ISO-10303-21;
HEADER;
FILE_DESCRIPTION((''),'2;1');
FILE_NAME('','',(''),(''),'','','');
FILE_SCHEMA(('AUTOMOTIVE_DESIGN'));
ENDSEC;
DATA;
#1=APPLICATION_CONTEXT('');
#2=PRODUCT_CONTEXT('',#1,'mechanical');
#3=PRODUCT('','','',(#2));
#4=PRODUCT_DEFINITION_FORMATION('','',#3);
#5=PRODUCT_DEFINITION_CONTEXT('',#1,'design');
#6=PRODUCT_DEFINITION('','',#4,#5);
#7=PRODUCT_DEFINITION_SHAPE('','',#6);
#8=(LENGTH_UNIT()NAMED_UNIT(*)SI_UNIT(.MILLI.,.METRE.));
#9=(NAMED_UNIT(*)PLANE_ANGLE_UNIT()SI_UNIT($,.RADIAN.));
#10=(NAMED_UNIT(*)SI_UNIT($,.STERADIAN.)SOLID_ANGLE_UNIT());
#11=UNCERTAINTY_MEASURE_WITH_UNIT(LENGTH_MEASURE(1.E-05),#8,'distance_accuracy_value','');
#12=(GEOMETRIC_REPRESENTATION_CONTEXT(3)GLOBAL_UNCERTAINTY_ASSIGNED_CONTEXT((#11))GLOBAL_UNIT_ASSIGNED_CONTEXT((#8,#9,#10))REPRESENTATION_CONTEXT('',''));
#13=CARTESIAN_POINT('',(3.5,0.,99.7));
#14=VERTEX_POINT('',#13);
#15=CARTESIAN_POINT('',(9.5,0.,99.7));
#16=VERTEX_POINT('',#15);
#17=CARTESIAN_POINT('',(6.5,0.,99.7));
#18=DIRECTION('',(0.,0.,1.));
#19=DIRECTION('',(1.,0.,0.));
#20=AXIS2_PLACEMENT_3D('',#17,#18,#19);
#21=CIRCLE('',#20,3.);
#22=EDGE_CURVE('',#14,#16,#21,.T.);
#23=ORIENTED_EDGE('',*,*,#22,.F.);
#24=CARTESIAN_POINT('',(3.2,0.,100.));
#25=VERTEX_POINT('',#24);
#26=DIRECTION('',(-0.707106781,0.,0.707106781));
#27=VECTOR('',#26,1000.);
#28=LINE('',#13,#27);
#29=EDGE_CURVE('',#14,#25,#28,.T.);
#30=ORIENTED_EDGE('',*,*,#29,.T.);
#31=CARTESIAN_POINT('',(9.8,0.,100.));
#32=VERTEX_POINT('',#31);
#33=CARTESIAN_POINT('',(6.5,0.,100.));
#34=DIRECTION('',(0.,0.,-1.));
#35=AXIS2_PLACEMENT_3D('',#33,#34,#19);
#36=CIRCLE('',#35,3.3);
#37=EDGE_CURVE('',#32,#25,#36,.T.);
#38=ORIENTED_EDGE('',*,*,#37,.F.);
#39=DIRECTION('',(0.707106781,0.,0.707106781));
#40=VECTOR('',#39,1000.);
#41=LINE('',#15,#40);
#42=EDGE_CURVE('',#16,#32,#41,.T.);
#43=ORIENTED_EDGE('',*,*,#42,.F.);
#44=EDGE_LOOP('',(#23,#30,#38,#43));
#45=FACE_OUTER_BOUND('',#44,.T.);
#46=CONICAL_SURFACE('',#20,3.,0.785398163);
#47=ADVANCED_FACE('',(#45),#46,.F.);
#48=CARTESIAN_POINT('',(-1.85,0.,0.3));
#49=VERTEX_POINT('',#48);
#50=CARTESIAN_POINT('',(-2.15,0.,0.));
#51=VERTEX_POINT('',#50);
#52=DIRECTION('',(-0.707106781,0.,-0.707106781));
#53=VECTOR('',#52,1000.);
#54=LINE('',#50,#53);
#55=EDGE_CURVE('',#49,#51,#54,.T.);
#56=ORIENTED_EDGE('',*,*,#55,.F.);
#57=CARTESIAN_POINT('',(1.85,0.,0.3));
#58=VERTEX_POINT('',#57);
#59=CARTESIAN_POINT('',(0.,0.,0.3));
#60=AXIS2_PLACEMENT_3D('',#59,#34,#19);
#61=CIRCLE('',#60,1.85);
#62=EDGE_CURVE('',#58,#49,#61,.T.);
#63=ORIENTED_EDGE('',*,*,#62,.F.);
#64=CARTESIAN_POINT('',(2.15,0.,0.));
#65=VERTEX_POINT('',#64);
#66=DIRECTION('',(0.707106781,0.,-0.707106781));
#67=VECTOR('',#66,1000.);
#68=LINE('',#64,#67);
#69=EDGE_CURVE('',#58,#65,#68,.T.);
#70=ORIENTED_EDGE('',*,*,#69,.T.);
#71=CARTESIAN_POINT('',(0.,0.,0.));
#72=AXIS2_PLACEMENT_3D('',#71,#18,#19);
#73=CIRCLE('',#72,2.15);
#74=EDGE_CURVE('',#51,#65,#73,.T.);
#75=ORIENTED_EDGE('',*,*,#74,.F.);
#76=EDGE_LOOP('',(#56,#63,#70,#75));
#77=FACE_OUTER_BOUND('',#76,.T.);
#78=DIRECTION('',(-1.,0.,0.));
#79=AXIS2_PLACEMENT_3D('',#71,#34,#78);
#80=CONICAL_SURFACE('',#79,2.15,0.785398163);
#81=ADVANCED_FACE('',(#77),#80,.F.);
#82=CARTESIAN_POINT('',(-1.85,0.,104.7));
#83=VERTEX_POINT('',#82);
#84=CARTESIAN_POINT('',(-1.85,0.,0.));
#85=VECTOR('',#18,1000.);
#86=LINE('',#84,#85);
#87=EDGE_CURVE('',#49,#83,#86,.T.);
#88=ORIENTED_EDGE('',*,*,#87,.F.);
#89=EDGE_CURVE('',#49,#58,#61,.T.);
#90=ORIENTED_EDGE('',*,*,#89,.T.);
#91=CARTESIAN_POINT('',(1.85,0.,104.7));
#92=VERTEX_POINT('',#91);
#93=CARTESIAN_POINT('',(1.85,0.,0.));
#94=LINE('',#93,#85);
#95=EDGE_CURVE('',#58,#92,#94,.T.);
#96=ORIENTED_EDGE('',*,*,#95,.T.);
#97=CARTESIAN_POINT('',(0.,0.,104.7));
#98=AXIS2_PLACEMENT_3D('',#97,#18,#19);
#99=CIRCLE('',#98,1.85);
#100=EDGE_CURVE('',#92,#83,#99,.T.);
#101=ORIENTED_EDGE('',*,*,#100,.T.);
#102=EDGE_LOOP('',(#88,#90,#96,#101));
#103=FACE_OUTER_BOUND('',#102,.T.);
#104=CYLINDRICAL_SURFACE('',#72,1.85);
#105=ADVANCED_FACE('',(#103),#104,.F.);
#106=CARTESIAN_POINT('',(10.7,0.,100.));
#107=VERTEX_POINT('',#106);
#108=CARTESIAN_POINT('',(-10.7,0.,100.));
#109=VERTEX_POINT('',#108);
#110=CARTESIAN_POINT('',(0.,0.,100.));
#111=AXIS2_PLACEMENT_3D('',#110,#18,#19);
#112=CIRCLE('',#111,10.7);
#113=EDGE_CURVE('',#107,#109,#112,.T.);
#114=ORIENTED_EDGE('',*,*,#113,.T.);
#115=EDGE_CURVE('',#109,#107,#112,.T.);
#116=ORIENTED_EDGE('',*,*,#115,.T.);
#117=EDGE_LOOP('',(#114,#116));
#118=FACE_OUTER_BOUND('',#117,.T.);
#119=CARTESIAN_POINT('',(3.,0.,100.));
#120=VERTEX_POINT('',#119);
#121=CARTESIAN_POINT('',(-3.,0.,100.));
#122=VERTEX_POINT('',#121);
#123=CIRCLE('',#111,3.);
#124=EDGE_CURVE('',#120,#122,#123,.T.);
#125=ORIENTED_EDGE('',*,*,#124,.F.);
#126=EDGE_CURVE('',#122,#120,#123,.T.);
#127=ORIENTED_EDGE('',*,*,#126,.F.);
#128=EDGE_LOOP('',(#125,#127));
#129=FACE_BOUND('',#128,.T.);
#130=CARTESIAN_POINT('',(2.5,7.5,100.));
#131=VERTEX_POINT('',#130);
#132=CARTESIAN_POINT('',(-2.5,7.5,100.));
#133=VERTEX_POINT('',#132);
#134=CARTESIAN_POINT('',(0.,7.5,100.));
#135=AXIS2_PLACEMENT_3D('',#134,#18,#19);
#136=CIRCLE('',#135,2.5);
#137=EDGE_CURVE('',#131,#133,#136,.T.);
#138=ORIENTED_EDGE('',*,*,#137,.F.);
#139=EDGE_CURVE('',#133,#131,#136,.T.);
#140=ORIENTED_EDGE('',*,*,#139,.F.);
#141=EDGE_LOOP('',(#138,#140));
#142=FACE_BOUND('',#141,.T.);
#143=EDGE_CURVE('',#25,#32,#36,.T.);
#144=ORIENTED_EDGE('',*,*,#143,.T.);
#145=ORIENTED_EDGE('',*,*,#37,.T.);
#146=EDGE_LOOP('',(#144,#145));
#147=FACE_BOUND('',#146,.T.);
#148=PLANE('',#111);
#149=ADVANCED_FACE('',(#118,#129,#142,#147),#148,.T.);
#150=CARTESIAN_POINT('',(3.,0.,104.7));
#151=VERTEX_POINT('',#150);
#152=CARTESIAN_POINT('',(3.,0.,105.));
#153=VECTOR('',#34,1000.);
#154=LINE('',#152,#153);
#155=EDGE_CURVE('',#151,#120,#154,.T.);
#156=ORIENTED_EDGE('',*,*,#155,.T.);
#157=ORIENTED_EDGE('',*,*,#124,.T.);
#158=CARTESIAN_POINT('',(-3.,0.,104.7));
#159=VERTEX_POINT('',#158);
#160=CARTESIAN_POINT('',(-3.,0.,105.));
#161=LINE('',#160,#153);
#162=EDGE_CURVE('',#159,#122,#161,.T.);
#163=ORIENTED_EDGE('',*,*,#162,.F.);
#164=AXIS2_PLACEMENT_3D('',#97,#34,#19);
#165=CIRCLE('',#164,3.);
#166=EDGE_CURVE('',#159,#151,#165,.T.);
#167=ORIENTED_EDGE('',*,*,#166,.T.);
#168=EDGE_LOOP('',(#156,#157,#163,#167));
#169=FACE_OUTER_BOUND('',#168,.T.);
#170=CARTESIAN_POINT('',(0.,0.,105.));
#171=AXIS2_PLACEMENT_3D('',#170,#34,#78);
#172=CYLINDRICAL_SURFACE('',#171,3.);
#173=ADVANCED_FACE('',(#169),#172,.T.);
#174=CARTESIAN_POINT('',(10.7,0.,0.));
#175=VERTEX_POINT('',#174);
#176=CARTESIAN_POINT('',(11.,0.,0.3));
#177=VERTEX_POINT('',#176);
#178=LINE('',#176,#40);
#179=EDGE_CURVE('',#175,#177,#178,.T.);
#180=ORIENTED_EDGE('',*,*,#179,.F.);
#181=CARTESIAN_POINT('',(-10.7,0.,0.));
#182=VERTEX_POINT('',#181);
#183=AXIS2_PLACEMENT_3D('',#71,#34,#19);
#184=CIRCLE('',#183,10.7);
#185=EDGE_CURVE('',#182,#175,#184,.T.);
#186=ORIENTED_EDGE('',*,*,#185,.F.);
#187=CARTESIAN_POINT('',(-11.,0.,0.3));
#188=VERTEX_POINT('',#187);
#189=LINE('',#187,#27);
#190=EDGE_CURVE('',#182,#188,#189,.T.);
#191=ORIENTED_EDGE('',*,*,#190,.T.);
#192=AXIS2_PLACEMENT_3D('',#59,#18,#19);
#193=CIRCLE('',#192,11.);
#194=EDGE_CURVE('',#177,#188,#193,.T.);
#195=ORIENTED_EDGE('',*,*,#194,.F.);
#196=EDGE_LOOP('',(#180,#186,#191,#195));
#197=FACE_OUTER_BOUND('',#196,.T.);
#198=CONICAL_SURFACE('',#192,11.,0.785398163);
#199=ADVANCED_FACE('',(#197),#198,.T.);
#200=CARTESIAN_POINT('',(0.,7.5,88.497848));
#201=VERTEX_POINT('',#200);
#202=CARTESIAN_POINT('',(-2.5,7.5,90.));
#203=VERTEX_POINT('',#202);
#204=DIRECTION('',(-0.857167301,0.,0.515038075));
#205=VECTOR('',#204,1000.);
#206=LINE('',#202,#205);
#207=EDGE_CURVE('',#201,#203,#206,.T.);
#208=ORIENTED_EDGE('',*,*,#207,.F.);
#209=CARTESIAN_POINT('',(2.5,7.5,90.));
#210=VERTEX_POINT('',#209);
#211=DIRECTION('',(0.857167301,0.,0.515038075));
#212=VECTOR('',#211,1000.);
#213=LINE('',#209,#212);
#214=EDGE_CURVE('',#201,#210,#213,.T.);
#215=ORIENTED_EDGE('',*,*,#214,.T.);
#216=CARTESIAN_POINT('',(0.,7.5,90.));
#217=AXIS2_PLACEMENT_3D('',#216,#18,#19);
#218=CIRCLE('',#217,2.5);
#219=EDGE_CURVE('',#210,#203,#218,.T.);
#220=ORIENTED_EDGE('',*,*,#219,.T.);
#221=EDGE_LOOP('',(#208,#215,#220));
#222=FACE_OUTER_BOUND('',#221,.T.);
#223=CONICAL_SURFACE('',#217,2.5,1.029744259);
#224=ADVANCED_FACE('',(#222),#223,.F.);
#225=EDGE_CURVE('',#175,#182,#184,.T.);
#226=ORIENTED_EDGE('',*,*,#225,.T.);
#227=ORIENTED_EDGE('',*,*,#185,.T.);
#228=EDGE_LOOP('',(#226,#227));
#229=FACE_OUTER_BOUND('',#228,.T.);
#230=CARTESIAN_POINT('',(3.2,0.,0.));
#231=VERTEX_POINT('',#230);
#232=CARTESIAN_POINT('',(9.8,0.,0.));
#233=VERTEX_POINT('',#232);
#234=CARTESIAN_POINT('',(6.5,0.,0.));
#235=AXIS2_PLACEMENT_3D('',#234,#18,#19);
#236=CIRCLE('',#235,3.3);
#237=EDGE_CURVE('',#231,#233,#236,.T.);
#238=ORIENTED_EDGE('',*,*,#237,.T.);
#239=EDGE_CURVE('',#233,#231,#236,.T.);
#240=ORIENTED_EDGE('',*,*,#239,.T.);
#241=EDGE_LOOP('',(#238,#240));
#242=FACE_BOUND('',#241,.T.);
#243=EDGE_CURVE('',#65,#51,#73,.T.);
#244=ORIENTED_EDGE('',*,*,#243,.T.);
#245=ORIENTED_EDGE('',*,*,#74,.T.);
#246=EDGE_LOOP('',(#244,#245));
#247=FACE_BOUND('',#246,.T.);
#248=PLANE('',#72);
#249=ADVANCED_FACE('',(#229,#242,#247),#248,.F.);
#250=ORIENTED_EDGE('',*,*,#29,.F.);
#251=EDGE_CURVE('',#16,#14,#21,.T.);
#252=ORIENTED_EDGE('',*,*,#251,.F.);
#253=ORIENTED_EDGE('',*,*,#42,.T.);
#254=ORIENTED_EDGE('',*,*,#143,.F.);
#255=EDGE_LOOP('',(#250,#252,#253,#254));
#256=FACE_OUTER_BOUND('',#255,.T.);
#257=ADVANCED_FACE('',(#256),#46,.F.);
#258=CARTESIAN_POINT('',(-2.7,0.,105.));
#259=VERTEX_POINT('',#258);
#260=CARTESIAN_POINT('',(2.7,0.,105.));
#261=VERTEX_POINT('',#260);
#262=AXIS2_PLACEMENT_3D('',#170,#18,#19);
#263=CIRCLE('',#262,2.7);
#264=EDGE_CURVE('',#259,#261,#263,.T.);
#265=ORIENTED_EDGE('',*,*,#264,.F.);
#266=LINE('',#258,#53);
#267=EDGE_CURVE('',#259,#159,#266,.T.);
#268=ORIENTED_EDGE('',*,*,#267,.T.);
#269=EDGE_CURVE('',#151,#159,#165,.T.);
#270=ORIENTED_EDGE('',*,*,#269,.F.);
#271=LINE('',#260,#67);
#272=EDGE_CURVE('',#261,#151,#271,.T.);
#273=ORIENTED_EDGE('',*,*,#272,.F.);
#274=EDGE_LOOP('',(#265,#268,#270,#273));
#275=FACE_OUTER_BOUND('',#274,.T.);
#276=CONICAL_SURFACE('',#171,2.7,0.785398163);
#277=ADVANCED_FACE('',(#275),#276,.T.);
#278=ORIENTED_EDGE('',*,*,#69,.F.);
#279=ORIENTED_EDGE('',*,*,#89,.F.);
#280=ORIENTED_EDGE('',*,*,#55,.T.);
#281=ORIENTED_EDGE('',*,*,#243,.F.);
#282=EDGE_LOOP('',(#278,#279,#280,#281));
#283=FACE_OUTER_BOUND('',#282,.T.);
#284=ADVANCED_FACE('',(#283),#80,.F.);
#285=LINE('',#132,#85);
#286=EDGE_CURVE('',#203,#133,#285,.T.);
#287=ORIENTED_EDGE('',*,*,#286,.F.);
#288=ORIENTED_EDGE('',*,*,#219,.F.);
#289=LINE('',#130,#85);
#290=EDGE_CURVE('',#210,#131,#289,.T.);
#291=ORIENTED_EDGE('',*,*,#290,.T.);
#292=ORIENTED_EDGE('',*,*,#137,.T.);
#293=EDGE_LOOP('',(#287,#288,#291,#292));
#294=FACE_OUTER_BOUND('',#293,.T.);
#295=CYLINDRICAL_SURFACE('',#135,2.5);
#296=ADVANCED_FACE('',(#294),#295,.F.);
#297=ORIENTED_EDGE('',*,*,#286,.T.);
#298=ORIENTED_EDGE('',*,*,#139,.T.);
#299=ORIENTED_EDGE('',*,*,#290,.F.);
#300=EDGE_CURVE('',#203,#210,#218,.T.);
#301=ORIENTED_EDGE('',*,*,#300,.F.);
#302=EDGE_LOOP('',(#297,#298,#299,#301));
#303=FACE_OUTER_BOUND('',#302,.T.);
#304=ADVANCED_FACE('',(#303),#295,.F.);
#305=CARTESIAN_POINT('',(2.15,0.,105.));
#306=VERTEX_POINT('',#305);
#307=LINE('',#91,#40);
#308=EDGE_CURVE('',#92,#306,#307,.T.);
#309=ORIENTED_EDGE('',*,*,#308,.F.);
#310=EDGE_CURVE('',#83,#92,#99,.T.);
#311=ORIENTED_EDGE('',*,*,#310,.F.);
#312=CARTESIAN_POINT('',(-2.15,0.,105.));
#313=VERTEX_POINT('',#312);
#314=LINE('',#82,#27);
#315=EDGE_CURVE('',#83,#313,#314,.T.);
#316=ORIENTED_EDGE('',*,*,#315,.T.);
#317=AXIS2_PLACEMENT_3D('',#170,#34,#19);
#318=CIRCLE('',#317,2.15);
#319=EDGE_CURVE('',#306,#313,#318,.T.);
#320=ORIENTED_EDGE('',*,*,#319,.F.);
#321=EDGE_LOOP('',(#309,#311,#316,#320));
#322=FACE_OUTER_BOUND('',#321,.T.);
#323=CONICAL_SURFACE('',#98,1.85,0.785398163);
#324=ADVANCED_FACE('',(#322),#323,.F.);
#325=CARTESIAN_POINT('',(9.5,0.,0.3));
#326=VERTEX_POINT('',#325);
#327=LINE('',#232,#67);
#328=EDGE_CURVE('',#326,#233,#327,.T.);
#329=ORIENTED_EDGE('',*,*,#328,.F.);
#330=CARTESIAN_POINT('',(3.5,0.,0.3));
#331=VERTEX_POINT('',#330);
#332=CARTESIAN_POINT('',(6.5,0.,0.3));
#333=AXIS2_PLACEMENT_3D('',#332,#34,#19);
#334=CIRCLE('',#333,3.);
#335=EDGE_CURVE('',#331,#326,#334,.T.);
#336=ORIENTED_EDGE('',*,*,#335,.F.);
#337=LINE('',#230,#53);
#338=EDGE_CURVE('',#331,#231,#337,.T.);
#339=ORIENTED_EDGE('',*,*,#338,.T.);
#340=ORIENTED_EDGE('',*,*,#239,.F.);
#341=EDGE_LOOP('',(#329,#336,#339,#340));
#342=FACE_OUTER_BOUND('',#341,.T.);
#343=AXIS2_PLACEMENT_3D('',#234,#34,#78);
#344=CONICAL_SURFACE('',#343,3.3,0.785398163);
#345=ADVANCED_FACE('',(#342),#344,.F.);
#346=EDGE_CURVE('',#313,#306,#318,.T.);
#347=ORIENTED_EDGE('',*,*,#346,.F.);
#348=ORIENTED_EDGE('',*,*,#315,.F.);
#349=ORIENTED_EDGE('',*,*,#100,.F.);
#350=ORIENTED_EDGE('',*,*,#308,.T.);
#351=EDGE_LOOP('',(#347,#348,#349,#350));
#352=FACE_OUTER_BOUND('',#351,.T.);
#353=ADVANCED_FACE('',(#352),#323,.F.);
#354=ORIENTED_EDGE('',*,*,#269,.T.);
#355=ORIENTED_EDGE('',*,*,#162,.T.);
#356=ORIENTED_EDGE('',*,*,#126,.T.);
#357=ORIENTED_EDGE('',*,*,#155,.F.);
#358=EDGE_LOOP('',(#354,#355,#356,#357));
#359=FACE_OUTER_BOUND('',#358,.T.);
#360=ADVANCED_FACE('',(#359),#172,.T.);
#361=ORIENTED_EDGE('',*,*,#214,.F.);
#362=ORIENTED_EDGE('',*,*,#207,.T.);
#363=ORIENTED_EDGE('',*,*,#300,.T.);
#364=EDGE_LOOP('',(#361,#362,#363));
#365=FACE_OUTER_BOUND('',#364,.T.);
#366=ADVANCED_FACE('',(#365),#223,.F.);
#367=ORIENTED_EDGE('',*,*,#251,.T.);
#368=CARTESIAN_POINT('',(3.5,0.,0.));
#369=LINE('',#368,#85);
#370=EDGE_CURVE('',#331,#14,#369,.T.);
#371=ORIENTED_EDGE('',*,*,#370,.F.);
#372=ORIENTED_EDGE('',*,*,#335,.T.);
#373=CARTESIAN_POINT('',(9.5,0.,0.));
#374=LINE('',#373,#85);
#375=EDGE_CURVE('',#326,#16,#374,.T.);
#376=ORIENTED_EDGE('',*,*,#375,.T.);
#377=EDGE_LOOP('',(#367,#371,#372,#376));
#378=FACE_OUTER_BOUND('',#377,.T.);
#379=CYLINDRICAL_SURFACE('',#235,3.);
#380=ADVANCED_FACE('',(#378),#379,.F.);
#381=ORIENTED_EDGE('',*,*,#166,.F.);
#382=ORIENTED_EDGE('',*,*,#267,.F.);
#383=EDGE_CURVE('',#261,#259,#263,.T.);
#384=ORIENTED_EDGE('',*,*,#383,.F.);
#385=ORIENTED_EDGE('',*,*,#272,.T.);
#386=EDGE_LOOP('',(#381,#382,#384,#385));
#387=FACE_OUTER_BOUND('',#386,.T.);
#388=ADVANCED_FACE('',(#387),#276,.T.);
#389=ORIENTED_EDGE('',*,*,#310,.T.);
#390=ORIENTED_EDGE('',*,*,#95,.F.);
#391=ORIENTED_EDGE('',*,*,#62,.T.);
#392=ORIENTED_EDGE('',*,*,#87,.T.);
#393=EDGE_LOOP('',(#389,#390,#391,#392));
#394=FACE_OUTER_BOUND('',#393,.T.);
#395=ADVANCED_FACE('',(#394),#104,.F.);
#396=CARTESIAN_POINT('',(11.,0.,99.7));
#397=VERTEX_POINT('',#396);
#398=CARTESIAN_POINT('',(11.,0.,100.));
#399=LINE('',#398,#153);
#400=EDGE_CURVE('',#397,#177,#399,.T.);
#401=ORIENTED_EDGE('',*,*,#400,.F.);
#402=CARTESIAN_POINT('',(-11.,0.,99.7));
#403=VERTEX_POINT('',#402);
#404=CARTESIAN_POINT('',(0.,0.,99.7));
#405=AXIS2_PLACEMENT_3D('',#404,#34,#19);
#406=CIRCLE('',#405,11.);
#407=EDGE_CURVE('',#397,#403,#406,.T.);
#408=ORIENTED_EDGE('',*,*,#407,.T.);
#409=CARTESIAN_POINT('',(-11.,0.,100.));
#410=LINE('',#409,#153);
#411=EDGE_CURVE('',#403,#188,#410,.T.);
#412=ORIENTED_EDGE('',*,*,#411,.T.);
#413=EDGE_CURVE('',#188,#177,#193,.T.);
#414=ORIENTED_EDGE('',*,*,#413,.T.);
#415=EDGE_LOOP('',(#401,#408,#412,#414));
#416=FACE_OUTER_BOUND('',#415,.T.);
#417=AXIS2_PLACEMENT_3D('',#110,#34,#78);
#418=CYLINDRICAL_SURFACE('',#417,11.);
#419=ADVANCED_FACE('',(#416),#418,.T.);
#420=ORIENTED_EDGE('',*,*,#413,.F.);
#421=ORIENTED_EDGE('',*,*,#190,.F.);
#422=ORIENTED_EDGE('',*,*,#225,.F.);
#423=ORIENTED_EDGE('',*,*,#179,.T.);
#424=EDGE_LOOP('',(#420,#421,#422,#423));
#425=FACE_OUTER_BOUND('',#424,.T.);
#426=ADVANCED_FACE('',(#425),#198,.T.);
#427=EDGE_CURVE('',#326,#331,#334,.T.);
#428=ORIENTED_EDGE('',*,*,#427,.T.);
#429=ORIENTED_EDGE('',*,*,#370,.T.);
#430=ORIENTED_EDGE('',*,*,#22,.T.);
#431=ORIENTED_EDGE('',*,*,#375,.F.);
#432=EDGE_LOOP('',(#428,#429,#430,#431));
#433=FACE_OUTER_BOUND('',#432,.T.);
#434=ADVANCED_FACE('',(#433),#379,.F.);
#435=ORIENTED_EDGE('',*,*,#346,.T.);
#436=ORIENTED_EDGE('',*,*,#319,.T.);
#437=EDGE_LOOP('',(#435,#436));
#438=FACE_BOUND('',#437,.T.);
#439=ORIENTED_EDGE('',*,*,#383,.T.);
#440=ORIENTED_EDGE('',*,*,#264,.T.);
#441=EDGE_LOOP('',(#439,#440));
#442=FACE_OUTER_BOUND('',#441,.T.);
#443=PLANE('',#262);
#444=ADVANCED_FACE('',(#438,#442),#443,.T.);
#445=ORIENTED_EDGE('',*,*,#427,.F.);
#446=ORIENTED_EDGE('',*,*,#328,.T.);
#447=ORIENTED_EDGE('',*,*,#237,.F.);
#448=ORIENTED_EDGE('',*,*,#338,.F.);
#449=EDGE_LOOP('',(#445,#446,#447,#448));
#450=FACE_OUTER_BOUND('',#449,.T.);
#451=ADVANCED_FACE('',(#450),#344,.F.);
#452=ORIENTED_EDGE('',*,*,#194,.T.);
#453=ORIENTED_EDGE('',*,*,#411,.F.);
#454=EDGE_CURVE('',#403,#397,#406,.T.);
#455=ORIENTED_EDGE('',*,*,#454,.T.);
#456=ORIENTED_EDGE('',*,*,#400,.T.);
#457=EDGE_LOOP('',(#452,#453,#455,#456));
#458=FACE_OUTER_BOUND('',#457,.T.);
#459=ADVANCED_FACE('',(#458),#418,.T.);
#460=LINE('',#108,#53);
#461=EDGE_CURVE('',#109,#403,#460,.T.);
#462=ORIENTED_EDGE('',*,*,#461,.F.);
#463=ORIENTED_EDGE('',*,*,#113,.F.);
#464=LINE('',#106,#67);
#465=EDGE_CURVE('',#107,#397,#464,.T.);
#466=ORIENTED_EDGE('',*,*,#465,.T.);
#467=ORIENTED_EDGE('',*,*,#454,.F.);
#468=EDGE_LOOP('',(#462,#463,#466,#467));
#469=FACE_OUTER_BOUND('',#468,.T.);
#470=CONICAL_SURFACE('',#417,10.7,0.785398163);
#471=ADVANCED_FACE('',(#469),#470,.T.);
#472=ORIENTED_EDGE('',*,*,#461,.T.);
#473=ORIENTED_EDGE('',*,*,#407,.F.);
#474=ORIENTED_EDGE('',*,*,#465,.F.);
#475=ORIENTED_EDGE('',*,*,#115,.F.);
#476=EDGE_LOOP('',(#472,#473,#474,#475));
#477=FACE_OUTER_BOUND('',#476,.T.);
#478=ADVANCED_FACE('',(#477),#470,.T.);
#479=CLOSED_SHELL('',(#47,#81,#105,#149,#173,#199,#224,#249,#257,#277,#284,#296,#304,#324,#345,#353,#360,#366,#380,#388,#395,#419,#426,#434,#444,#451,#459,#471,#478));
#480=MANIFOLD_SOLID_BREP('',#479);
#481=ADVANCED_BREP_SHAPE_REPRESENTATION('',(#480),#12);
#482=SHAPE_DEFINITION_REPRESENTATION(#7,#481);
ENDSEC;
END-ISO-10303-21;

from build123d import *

# Parameters (mm, degrees)
SKETCH1_R             = 11
BOSS_EXTRUDE1_DEPTH   = 100
SKETCH2_R             = 3
BOSS_EXTRUDE2_DEPTH   = 5
SKETCH3_R             = 1.85
CUT_EXTRUDE1_DEPTH    = 107.146125695
SKETCH4_R             = 3
CUT_EXTRUDE2_DEPTH    = 102.202766761
M6_TAPPED_HOLE1_D     = 5
M6_TAPPED_HOLE1_DEPTH = 10
M6_TAPPED_HOLE1_TIP   = 1.502151548
CHAMFER1_SIZE         = 0.3


with BuildPart() as part:
    # Sketch1 → Boss-Extrude1 (new body)
    with BuildSketch(Plane.XY):
        Circle(SKETCH1_R)
    extrude(amount=BOSS_EXTRUDE1_DEPTH)

    # Sketch2 → Boss-Extrude2 (add)
    with BuildSketch(Plane.XY.offset(100)):
        Circle(SKETCH2_R)
    extrude(amount=BOSS_EXTRUDE2_DEPTH)

    # Sketch3 → Cut-Extrude1 (cut, through all)
    with BuildSketch(Plane.XY.offset(105)):
        Circle(SKETCH3_R)
    extrude(amount=-CUT_EXTRUDE1_DEPTH, mode=Mode.SUBTRACT)

    # Sketch4 → Cut-Extrude2 (cut, through all)
    with BuildSketch(Plane.XY.offset(100)):
        with Locations((6.5, 0)):
            Circle(SKETCH4_R)
    extrude(amount=-CUT_EXTRUDE2_DEPTH, mode=Mode.SUBTRACT)

    # M6 Tapped Hole1
    with Locations(Plane.XY.offset(100)):
        with Locations((0, 7.5)):
            Hole(M6_TAPPED_HOLE1_D / 2, depth=M6_TAPPED_HOLE1_DEPTH)
            with Locations((0, 0, -(M6_TAPPED_HOLE1_DEPTH + M6_TAPPED_HOLE1_TIP / 2))):  # 118° drill point
                Cone(0, M6_TAPPED_HOLE1_D / 2, M6_TAPPED_HOLE1_TIP, mode=Mode.SUBTRACT)

    # Chamfer1
    chamfer1_edges = [part.edges().sort_by_distance(p)[0] for p in [
        (-1.85, 0, 0),
        (-1.85, 0, 105),
        (3.5, 0, 0),
        (3.5, 0, 100),
        (-11, 0, 0),
        (-11, 0, 100),
        (-3, 0, 105),
    ]]
    chamfer(chamfer1_edges, length=CHAMFER1_SIZE)


solid = part.part
